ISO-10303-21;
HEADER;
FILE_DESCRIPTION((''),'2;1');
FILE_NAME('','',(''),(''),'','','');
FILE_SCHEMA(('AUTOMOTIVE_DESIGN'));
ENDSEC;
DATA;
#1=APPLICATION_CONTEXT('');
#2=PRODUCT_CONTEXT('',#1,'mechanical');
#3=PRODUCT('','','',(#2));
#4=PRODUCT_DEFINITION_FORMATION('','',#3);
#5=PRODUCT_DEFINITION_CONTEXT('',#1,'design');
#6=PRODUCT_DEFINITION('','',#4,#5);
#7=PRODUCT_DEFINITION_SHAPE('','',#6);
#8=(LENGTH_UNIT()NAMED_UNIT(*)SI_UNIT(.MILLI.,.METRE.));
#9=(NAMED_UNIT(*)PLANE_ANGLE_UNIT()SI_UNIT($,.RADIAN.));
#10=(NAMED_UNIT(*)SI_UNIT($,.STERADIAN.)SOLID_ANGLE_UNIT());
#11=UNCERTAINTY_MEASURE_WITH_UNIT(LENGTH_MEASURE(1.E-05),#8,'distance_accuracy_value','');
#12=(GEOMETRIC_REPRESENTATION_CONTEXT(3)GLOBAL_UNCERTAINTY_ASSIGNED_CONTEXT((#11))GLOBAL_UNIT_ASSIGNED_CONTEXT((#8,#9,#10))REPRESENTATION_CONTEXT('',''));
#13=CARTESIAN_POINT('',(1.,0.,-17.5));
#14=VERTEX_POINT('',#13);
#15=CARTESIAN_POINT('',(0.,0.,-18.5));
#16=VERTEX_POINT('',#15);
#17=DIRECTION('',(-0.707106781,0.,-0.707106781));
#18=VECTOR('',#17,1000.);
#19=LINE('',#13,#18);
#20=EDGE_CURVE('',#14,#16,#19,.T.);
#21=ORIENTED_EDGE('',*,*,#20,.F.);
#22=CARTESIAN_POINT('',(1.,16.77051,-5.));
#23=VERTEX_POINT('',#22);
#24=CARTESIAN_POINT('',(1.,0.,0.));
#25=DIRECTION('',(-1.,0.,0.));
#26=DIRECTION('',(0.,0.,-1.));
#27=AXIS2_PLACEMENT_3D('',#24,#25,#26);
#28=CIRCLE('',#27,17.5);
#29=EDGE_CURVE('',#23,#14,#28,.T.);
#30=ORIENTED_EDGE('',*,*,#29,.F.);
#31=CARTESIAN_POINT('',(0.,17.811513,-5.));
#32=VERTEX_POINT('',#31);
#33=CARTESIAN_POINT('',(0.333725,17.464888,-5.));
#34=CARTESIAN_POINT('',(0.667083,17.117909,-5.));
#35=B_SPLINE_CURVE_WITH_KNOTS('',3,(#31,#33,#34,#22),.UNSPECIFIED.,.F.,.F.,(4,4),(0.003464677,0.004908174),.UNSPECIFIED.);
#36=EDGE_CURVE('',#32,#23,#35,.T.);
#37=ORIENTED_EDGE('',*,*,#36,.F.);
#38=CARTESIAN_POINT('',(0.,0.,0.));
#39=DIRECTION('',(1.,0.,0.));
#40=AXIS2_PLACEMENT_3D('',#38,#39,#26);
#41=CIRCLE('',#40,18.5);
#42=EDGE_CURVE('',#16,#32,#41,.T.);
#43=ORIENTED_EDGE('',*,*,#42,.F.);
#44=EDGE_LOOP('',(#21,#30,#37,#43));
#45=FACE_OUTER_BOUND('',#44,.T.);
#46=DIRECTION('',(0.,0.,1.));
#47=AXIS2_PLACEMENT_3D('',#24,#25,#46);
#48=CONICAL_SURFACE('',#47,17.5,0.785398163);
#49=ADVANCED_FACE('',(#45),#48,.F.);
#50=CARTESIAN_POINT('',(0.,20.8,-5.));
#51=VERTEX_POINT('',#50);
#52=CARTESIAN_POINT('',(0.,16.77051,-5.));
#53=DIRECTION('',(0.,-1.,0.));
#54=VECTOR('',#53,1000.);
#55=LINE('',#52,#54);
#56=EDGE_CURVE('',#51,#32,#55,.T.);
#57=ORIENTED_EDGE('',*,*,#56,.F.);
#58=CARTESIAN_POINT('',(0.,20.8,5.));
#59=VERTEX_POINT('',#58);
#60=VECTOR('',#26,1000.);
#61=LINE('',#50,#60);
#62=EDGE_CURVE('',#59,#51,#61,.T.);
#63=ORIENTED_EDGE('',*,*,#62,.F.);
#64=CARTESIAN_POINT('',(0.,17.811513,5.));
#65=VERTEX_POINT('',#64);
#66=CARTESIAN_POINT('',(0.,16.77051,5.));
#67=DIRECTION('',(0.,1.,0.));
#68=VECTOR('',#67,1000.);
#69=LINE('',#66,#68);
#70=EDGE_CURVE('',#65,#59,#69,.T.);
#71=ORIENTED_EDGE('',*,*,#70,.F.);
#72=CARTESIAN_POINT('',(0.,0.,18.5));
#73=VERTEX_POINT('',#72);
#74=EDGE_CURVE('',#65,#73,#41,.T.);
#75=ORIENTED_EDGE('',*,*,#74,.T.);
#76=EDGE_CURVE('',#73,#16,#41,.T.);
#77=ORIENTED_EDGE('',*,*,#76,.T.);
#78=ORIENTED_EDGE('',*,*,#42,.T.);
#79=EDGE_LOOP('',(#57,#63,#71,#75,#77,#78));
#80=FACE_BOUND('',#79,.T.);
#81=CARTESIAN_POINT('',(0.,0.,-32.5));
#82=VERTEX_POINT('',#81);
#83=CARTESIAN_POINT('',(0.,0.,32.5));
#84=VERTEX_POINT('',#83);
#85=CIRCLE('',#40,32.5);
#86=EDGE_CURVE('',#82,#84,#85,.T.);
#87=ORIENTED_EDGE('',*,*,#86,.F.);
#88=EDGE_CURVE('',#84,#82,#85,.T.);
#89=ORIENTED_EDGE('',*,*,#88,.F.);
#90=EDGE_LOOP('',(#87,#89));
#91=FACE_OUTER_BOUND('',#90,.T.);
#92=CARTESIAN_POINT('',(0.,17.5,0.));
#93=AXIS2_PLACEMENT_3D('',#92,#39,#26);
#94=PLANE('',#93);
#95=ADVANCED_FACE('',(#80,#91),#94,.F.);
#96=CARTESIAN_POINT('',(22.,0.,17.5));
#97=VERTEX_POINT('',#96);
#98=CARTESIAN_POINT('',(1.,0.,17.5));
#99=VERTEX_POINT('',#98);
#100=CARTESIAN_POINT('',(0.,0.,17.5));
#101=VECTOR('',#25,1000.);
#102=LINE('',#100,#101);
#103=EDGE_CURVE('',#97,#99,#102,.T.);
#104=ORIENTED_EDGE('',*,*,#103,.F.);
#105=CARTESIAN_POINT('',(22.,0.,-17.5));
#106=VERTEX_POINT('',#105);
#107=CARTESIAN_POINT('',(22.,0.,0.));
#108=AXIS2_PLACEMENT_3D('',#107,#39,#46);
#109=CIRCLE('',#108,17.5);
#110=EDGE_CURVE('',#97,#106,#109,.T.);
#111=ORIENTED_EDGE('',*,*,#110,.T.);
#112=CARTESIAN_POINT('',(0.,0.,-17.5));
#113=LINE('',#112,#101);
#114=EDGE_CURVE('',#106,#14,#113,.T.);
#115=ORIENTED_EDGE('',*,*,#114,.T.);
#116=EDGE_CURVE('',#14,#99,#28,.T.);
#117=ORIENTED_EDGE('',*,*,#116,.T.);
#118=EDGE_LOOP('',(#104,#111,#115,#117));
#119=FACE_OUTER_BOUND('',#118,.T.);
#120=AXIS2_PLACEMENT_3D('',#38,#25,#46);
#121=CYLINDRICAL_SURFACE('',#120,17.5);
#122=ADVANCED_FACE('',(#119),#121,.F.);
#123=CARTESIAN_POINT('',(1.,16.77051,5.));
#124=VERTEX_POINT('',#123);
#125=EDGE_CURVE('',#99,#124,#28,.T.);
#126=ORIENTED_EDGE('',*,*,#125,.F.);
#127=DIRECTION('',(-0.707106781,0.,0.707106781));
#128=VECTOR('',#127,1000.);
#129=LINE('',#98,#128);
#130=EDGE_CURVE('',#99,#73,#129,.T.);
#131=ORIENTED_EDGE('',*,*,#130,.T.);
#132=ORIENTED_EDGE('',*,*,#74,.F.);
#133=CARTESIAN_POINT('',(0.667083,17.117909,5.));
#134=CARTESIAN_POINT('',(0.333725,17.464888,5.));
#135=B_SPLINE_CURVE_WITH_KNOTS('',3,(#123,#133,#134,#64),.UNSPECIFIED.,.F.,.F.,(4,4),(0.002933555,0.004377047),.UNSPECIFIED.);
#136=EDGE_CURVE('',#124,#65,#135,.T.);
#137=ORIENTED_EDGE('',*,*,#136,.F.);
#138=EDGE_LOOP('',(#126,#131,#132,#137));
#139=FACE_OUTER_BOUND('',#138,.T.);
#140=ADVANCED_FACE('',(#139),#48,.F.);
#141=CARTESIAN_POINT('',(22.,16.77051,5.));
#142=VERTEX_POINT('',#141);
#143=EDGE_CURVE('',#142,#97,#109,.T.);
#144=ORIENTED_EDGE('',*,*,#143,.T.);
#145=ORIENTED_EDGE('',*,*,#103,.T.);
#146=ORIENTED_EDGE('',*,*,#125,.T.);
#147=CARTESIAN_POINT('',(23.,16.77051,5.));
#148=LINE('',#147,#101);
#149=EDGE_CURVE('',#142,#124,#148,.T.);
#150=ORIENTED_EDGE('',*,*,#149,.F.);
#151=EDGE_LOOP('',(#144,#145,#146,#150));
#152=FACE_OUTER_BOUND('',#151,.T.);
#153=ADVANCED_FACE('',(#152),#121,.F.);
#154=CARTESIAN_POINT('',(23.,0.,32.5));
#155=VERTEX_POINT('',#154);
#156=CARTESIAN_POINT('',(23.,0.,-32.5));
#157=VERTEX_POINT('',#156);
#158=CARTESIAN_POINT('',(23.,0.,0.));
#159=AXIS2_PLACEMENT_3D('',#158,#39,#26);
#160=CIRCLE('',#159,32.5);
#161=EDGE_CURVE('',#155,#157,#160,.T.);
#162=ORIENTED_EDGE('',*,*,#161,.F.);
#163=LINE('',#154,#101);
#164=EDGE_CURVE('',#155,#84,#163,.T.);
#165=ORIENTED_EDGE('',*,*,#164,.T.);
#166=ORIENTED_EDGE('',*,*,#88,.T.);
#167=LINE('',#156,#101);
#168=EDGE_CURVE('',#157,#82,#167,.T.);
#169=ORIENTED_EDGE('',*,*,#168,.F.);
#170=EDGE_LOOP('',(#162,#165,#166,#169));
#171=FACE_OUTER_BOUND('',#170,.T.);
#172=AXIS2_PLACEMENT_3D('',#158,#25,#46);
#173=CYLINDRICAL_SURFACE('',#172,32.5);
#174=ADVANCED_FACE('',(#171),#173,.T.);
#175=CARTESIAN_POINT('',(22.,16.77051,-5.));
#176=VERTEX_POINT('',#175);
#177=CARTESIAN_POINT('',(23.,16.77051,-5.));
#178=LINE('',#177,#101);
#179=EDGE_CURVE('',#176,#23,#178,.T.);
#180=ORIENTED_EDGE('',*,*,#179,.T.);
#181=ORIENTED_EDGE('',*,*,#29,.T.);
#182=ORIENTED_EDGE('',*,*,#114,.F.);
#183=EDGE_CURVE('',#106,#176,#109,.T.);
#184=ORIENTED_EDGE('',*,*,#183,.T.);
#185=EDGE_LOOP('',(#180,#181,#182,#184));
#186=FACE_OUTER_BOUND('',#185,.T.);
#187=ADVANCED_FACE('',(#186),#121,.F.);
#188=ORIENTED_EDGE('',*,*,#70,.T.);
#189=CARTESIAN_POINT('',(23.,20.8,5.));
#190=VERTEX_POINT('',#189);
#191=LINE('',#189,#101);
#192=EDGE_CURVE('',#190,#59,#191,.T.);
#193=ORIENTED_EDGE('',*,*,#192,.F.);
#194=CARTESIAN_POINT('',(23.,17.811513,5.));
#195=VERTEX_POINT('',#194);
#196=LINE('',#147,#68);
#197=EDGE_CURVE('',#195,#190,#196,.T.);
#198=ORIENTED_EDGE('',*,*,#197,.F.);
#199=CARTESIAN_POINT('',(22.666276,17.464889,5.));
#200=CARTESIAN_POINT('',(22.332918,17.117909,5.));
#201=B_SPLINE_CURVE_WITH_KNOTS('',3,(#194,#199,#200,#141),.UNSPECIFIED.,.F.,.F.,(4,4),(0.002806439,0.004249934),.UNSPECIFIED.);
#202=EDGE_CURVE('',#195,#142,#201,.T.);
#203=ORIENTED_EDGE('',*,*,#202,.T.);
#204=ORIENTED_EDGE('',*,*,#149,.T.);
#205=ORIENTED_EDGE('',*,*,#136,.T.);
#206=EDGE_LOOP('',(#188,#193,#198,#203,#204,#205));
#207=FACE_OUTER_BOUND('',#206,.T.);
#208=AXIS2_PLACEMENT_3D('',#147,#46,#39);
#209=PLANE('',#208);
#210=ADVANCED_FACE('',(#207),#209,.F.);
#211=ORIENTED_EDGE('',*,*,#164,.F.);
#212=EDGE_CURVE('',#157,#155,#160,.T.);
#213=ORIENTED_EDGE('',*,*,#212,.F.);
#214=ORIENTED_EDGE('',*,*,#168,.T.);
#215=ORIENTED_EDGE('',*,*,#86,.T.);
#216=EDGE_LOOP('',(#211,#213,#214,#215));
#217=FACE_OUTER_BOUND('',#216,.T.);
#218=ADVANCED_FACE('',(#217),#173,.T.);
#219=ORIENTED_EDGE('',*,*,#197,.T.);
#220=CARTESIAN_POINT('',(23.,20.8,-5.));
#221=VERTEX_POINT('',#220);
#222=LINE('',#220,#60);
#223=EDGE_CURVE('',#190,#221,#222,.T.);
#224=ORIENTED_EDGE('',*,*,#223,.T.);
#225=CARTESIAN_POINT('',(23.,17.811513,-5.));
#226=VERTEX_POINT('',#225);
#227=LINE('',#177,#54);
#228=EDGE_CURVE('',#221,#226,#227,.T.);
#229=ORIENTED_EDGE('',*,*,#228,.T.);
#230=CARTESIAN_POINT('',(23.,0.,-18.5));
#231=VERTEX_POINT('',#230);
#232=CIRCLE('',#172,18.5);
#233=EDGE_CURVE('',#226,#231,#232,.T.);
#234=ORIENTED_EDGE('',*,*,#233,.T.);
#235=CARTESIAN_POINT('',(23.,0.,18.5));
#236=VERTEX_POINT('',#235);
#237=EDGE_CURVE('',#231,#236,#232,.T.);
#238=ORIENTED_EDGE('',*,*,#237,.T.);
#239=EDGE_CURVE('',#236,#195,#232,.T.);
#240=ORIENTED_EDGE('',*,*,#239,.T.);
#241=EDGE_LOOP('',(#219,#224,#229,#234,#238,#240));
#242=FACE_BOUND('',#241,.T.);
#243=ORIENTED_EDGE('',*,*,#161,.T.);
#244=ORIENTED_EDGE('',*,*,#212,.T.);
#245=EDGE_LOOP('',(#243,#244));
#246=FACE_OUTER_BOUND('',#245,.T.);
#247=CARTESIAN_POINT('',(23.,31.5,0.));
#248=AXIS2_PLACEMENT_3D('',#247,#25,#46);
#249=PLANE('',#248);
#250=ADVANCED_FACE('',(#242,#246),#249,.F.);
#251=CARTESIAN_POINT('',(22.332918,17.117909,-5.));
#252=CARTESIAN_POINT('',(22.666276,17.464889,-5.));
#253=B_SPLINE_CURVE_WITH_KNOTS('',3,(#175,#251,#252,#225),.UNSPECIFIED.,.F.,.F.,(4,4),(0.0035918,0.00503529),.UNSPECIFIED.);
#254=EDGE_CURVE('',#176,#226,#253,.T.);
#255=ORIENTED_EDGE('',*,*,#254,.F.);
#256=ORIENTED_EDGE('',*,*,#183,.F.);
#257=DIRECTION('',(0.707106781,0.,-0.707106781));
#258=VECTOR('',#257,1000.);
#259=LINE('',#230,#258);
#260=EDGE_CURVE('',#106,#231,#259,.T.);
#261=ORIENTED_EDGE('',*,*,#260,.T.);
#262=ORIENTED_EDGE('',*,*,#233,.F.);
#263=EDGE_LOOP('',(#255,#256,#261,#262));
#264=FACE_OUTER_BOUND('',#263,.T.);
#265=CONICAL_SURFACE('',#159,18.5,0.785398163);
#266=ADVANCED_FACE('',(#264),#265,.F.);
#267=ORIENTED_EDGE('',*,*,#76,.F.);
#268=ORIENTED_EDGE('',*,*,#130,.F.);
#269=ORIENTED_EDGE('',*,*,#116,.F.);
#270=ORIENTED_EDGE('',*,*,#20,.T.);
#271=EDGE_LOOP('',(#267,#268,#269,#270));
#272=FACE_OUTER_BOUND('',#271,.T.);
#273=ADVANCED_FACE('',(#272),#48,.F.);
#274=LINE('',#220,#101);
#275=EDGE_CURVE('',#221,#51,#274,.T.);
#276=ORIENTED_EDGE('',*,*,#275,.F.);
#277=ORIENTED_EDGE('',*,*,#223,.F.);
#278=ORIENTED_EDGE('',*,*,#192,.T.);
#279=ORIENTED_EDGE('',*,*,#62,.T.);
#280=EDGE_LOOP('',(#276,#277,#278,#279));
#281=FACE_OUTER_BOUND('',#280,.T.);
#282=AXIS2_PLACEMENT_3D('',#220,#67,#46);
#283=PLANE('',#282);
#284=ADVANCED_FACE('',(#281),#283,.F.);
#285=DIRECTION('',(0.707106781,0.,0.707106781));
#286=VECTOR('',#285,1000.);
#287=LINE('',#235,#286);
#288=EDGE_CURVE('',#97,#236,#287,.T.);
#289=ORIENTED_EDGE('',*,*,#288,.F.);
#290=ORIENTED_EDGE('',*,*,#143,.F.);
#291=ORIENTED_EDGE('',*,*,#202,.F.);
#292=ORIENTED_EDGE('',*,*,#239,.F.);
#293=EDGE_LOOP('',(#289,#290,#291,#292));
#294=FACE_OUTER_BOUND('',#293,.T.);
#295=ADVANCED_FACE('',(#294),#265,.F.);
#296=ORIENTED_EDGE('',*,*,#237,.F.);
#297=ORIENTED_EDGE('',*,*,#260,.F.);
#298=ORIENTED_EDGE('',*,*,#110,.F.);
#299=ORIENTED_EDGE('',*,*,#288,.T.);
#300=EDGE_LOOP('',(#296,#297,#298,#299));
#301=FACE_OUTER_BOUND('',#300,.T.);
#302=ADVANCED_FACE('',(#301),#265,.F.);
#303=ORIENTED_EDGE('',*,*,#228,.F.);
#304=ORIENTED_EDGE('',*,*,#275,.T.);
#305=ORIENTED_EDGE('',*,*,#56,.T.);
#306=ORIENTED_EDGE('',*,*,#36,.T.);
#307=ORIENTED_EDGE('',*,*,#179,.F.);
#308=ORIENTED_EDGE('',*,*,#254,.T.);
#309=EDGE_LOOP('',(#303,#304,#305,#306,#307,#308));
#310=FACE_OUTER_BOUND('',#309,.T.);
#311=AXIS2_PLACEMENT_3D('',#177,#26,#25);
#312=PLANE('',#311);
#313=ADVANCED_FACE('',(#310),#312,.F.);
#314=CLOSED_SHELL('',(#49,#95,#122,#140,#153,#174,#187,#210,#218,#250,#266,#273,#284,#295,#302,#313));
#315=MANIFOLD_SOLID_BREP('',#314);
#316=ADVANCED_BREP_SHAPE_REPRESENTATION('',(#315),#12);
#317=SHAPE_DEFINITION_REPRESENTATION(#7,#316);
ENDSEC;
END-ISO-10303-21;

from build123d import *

# Parameters (mm, degrees)
CHAMFER_1_SIZE           = 1
SKETCH_4_W               = 10
SKETCH_4_H               = 4.029490121
CUT_EXTRUDE_1_DEPTH      = 69.000919111
CUT_EXTRUDE_3_DEPTH      = 23
CUT_EXTRUDE_3_DEPTH_BACK = 2
SKETCH_6_OUTSIDE_W       = 118.508
SKETCH_6_OUTSIDE_H       = 118.508
SKETCH_6_OUTSIDE_R       = 31.5
SKETCH_9_R               = 32.5
SKETCH_9_R_2             = 31.5
EXTRUDE_1_DEPTH          = 23


with BuildPart() as part:
    # 草图1 → 旋转1 (revolve)
    with BuildSketch(Plane.XY, mode=Mode.PRIVATE) as revolve_1_sk:
        Polygon((0, 17.5), (0, 45.25), (18, 45.25), (18, 31.5), (23, 31.5), (23, 17.5), align=None)
    revolve(revolve_1_sk.sketch.rotate(Axis((0, 0, 0), (1, 0, 0)), 90), axis=Axis((0, 0, 0), (1, 0, 0)))

    # 草图2 → 切除-旋转1 (revolve, cut)
    with BuildSketch(Plane.XY, mode=Mode.PRIVATE) as cut_revolve_1_sk:
        Polygon((11.840143071, 33.8), (15.340759374, 45.25), (2.659240626, 45.25), (6.159856929, 33.8), align=None)
    revolve(cut_revolve_1_sk.sketch.rotate(Axis((0, 0, 0), (1, 0, 0)), 90), axis=Axis((0, 0, 0), (1, 0, 0)), mode=Mode.SUBTRACT)

    # 倒角1
    chamfer_1_edges = [part.edges().sort_by_distance(p)[0] for p in [
        (0, 0, -17.5),
        (23, 0, -17.5),
    ]]
    chamfer(chamfer_1_edges, length=CHAMFER_1_SIZE)

    # 草图4 → 切除-拉伸1 (cut, through all)
    with BuildSketch(Plane.ZY):
        with Locations((0, 18.785254892)):
            Rectangle(SKETCH_4_W, SKETCH_4_H)
    extrude(amount=-CUT_EXTRUDE_1_DEPTH, mode=Mode.SUBTRACT)

    # 草图6 outside → 切除-拉伸3 (cut, two sides: drawn at the far end of the back side and taken through both)
    with BuildSketch(Plane(origin=(0, 0, 0), x_dir=(0, 0, -1), z_dir=(1, 0, 0)).offset(-CUT_EXTRUDE_3_DEPTH_BACK)):
        Rectangle(SKETCH_6_OUTSIDE_W, SKETCH_6_OUTSIDE_H)
        with Locations(Location((0, 0, 0), (0, 0, 180))):
            Circle(SKETCH_6_OUTSIDE_R, mode=Mode.SUBTRACT)
    extrude(amount=CUT_EXTRUDE_3_DEPTH + CUT_EXTRUDE_3_DEPTH_BACK, mode=Mode.SUBTRACT)

    # 草图9 → 凸台-拉伸1 (add)
    with BuildSketch(Plane(origin=(0, 0, 0), x_dir=(0, 0, -1), z_dir=(1, 0, 0))):
        Circle(SKETCH_9_R)
        Circle(SKETCH_9_R_2, mode=Mode.SUBTRACT)
    extrude(amount=EXTRUDE_1_DEPTH)


solid = part.part
